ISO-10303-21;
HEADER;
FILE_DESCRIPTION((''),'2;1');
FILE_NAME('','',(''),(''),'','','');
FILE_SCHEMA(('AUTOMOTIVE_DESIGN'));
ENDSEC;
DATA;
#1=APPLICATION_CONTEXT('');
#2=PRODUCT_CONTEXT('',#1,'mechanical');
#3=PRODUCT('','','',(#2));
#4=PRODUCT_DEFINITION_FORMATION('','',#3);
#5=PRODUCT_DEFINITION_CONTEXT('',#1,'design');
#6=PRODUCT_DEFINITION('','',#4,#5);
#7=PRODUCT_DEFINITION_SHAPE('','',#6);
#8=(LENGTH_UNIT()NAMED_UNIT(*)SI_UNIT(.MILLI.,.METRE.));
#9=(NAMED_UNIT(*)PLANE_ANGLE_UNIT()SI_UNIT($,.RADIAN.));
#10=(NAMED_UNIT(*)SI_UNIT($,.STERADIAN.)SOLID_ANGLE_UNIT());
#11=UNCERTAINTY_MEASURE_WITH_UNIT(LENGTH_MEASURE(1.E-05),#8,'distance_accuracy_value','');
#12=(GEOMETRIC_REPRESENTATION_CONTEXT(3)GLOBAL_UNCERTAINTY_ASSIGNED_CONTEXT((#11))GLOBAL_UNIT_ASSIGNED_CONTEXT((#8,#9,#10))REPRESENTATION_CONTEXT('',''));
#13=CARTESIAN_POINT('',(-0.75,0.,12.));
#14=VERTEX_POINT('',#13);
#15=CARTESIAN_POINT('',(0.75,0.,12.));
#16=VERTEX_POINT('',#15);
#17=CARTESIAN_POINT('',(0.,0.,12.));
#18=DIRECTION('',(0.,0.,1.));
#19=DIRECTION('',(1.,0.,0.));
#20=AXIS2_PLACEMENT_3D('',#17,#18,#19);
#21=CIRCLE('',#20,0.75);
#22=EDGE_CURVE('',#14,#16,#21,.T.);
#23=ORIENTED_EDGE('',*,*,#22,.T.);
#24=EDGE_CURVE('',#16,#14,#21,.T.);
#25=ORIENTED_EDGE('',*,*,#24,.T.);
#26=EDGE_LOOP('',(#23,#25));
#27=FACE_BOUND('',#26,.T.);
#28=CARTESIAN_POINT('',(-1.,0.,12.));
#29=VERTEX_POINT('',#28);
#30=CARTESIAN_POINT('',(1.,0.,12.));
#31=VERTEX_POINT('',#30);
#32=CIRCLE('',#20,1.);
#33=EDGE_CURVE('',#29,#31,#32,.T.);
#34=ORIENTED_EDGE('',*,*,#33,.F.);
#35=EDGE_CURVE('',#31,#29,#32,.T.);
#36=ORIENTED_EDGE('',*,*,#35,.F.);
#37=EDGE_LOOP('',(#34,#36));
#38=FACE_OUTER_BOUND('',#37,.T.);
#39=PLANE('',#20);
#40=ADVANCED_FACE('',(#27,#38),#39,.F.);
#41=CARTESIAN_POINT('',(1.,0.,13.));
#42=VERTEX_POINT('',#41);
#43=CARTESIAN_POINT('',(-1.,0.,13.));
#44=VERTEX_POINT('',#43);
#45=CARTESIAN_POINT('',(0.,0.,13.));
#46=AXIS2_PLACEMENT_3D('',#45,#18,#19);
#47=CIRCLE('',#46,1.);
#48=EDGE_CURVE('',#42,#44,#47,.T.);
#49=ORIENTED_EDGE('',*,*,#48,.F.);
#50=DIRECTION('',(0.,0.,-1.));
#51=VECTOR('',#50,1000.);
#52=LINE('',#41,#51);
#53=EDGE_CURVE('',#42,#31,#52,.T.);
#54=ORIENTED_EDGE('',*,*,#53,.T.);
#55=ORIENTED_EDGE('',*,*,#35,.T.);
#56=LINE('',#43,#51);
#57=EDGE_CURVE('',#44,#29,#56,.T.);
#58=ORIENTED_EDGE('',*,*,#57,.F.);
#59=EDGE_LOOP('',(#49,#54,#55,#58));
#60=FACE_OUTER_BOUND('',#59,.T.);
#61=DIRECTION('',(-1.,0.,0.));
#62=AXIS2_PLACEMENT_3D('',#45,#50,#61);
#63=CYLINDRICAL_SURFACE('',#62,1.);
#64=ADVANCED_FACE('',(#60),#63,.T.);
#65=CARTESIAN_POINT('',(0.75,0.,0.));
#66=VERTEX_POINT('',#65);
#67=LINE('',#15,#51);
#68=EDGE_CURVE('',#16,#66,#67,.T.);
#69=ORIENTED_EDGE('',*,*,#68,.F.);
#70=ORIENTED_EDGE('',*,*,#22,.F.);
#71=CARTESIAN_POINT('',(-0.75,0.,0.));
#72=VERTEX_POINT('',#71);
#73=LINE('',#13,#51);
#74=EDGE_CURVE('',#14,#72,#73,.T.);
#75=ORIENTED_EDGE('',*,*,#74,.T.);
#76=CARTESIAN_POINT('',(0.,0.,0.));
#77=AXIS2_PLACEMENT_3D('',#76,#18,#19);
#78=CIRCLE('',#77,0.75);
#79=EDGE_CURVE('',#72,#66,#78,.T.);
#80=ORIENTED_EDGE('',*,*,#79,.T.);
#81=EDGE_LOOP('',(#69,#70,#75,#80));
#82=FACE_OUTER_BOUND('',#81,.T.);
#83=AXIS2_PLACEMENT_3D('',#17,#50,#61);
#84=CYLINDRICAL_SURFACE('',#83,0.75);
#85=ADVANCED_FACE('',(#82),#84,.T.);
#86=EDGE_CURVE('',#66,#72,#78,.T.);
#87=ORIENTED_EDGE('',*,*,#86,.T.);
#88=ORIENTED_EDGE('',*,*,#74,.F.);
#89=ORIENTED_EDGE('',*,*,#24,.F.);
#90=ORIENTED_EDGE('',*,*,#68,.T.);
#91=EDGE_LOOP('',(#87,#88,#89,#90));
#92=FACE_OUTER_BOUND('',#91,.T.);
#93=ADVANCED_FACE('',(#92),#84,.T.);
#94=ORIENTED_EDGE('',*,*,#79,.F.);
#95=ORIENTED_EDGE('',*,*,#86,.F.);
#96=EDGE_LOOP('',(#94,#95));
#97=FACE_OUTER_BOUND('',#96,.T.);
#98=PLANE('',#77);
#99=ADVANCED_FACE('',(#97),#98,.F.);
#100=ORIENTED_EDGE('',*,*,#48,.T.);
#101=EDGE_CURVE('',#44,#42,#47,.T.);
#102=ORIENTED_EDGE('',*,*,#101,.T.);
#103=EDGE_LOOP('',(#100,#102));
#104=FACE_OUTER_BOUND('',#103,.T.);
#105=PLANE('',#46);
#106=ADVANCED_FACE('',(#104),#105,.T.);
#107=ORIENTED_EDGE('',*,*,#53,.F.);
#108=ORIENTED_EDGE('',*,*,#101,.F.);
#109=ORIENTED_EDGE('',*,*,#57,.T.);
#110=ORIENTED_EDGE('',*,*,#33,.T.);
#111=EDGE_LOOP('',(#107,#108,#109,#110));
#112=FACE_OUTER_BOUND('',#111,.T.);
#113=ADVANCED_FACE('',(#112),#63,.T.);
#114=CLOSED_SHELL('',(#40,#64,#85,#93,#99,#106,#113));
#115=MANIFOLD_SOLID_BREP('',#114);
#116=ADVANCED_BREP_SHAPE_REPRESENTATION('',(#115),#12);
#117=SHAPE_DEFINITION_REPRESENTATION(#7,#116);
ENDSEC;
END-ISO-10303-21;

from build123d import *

# Parameters (mm, degrees)
SKETCH_1_R      = 0.75
EXTRUDE_1_DEPTH = 12
SKETCH_2_R      = 1
EXTRUDE_2_DEPTH = 1


with BuildPart() as part:
    # 草图1 → 凸台-拉伸1 (new body)
    with BuildSketch(Plane.XY):
        Circle(SKETCH_1_R)
    extrude(amount=EXTRUDE_1_DEPTH)

    # 草图2 → 凸台-拉伸2 (add)
    with BuildSketch(Plane.XY.offset(12)):
        Circle(SKETCH_2_R)
    extrude(amount=EXTRUDE_2_DEPTH)


solid = part.part
